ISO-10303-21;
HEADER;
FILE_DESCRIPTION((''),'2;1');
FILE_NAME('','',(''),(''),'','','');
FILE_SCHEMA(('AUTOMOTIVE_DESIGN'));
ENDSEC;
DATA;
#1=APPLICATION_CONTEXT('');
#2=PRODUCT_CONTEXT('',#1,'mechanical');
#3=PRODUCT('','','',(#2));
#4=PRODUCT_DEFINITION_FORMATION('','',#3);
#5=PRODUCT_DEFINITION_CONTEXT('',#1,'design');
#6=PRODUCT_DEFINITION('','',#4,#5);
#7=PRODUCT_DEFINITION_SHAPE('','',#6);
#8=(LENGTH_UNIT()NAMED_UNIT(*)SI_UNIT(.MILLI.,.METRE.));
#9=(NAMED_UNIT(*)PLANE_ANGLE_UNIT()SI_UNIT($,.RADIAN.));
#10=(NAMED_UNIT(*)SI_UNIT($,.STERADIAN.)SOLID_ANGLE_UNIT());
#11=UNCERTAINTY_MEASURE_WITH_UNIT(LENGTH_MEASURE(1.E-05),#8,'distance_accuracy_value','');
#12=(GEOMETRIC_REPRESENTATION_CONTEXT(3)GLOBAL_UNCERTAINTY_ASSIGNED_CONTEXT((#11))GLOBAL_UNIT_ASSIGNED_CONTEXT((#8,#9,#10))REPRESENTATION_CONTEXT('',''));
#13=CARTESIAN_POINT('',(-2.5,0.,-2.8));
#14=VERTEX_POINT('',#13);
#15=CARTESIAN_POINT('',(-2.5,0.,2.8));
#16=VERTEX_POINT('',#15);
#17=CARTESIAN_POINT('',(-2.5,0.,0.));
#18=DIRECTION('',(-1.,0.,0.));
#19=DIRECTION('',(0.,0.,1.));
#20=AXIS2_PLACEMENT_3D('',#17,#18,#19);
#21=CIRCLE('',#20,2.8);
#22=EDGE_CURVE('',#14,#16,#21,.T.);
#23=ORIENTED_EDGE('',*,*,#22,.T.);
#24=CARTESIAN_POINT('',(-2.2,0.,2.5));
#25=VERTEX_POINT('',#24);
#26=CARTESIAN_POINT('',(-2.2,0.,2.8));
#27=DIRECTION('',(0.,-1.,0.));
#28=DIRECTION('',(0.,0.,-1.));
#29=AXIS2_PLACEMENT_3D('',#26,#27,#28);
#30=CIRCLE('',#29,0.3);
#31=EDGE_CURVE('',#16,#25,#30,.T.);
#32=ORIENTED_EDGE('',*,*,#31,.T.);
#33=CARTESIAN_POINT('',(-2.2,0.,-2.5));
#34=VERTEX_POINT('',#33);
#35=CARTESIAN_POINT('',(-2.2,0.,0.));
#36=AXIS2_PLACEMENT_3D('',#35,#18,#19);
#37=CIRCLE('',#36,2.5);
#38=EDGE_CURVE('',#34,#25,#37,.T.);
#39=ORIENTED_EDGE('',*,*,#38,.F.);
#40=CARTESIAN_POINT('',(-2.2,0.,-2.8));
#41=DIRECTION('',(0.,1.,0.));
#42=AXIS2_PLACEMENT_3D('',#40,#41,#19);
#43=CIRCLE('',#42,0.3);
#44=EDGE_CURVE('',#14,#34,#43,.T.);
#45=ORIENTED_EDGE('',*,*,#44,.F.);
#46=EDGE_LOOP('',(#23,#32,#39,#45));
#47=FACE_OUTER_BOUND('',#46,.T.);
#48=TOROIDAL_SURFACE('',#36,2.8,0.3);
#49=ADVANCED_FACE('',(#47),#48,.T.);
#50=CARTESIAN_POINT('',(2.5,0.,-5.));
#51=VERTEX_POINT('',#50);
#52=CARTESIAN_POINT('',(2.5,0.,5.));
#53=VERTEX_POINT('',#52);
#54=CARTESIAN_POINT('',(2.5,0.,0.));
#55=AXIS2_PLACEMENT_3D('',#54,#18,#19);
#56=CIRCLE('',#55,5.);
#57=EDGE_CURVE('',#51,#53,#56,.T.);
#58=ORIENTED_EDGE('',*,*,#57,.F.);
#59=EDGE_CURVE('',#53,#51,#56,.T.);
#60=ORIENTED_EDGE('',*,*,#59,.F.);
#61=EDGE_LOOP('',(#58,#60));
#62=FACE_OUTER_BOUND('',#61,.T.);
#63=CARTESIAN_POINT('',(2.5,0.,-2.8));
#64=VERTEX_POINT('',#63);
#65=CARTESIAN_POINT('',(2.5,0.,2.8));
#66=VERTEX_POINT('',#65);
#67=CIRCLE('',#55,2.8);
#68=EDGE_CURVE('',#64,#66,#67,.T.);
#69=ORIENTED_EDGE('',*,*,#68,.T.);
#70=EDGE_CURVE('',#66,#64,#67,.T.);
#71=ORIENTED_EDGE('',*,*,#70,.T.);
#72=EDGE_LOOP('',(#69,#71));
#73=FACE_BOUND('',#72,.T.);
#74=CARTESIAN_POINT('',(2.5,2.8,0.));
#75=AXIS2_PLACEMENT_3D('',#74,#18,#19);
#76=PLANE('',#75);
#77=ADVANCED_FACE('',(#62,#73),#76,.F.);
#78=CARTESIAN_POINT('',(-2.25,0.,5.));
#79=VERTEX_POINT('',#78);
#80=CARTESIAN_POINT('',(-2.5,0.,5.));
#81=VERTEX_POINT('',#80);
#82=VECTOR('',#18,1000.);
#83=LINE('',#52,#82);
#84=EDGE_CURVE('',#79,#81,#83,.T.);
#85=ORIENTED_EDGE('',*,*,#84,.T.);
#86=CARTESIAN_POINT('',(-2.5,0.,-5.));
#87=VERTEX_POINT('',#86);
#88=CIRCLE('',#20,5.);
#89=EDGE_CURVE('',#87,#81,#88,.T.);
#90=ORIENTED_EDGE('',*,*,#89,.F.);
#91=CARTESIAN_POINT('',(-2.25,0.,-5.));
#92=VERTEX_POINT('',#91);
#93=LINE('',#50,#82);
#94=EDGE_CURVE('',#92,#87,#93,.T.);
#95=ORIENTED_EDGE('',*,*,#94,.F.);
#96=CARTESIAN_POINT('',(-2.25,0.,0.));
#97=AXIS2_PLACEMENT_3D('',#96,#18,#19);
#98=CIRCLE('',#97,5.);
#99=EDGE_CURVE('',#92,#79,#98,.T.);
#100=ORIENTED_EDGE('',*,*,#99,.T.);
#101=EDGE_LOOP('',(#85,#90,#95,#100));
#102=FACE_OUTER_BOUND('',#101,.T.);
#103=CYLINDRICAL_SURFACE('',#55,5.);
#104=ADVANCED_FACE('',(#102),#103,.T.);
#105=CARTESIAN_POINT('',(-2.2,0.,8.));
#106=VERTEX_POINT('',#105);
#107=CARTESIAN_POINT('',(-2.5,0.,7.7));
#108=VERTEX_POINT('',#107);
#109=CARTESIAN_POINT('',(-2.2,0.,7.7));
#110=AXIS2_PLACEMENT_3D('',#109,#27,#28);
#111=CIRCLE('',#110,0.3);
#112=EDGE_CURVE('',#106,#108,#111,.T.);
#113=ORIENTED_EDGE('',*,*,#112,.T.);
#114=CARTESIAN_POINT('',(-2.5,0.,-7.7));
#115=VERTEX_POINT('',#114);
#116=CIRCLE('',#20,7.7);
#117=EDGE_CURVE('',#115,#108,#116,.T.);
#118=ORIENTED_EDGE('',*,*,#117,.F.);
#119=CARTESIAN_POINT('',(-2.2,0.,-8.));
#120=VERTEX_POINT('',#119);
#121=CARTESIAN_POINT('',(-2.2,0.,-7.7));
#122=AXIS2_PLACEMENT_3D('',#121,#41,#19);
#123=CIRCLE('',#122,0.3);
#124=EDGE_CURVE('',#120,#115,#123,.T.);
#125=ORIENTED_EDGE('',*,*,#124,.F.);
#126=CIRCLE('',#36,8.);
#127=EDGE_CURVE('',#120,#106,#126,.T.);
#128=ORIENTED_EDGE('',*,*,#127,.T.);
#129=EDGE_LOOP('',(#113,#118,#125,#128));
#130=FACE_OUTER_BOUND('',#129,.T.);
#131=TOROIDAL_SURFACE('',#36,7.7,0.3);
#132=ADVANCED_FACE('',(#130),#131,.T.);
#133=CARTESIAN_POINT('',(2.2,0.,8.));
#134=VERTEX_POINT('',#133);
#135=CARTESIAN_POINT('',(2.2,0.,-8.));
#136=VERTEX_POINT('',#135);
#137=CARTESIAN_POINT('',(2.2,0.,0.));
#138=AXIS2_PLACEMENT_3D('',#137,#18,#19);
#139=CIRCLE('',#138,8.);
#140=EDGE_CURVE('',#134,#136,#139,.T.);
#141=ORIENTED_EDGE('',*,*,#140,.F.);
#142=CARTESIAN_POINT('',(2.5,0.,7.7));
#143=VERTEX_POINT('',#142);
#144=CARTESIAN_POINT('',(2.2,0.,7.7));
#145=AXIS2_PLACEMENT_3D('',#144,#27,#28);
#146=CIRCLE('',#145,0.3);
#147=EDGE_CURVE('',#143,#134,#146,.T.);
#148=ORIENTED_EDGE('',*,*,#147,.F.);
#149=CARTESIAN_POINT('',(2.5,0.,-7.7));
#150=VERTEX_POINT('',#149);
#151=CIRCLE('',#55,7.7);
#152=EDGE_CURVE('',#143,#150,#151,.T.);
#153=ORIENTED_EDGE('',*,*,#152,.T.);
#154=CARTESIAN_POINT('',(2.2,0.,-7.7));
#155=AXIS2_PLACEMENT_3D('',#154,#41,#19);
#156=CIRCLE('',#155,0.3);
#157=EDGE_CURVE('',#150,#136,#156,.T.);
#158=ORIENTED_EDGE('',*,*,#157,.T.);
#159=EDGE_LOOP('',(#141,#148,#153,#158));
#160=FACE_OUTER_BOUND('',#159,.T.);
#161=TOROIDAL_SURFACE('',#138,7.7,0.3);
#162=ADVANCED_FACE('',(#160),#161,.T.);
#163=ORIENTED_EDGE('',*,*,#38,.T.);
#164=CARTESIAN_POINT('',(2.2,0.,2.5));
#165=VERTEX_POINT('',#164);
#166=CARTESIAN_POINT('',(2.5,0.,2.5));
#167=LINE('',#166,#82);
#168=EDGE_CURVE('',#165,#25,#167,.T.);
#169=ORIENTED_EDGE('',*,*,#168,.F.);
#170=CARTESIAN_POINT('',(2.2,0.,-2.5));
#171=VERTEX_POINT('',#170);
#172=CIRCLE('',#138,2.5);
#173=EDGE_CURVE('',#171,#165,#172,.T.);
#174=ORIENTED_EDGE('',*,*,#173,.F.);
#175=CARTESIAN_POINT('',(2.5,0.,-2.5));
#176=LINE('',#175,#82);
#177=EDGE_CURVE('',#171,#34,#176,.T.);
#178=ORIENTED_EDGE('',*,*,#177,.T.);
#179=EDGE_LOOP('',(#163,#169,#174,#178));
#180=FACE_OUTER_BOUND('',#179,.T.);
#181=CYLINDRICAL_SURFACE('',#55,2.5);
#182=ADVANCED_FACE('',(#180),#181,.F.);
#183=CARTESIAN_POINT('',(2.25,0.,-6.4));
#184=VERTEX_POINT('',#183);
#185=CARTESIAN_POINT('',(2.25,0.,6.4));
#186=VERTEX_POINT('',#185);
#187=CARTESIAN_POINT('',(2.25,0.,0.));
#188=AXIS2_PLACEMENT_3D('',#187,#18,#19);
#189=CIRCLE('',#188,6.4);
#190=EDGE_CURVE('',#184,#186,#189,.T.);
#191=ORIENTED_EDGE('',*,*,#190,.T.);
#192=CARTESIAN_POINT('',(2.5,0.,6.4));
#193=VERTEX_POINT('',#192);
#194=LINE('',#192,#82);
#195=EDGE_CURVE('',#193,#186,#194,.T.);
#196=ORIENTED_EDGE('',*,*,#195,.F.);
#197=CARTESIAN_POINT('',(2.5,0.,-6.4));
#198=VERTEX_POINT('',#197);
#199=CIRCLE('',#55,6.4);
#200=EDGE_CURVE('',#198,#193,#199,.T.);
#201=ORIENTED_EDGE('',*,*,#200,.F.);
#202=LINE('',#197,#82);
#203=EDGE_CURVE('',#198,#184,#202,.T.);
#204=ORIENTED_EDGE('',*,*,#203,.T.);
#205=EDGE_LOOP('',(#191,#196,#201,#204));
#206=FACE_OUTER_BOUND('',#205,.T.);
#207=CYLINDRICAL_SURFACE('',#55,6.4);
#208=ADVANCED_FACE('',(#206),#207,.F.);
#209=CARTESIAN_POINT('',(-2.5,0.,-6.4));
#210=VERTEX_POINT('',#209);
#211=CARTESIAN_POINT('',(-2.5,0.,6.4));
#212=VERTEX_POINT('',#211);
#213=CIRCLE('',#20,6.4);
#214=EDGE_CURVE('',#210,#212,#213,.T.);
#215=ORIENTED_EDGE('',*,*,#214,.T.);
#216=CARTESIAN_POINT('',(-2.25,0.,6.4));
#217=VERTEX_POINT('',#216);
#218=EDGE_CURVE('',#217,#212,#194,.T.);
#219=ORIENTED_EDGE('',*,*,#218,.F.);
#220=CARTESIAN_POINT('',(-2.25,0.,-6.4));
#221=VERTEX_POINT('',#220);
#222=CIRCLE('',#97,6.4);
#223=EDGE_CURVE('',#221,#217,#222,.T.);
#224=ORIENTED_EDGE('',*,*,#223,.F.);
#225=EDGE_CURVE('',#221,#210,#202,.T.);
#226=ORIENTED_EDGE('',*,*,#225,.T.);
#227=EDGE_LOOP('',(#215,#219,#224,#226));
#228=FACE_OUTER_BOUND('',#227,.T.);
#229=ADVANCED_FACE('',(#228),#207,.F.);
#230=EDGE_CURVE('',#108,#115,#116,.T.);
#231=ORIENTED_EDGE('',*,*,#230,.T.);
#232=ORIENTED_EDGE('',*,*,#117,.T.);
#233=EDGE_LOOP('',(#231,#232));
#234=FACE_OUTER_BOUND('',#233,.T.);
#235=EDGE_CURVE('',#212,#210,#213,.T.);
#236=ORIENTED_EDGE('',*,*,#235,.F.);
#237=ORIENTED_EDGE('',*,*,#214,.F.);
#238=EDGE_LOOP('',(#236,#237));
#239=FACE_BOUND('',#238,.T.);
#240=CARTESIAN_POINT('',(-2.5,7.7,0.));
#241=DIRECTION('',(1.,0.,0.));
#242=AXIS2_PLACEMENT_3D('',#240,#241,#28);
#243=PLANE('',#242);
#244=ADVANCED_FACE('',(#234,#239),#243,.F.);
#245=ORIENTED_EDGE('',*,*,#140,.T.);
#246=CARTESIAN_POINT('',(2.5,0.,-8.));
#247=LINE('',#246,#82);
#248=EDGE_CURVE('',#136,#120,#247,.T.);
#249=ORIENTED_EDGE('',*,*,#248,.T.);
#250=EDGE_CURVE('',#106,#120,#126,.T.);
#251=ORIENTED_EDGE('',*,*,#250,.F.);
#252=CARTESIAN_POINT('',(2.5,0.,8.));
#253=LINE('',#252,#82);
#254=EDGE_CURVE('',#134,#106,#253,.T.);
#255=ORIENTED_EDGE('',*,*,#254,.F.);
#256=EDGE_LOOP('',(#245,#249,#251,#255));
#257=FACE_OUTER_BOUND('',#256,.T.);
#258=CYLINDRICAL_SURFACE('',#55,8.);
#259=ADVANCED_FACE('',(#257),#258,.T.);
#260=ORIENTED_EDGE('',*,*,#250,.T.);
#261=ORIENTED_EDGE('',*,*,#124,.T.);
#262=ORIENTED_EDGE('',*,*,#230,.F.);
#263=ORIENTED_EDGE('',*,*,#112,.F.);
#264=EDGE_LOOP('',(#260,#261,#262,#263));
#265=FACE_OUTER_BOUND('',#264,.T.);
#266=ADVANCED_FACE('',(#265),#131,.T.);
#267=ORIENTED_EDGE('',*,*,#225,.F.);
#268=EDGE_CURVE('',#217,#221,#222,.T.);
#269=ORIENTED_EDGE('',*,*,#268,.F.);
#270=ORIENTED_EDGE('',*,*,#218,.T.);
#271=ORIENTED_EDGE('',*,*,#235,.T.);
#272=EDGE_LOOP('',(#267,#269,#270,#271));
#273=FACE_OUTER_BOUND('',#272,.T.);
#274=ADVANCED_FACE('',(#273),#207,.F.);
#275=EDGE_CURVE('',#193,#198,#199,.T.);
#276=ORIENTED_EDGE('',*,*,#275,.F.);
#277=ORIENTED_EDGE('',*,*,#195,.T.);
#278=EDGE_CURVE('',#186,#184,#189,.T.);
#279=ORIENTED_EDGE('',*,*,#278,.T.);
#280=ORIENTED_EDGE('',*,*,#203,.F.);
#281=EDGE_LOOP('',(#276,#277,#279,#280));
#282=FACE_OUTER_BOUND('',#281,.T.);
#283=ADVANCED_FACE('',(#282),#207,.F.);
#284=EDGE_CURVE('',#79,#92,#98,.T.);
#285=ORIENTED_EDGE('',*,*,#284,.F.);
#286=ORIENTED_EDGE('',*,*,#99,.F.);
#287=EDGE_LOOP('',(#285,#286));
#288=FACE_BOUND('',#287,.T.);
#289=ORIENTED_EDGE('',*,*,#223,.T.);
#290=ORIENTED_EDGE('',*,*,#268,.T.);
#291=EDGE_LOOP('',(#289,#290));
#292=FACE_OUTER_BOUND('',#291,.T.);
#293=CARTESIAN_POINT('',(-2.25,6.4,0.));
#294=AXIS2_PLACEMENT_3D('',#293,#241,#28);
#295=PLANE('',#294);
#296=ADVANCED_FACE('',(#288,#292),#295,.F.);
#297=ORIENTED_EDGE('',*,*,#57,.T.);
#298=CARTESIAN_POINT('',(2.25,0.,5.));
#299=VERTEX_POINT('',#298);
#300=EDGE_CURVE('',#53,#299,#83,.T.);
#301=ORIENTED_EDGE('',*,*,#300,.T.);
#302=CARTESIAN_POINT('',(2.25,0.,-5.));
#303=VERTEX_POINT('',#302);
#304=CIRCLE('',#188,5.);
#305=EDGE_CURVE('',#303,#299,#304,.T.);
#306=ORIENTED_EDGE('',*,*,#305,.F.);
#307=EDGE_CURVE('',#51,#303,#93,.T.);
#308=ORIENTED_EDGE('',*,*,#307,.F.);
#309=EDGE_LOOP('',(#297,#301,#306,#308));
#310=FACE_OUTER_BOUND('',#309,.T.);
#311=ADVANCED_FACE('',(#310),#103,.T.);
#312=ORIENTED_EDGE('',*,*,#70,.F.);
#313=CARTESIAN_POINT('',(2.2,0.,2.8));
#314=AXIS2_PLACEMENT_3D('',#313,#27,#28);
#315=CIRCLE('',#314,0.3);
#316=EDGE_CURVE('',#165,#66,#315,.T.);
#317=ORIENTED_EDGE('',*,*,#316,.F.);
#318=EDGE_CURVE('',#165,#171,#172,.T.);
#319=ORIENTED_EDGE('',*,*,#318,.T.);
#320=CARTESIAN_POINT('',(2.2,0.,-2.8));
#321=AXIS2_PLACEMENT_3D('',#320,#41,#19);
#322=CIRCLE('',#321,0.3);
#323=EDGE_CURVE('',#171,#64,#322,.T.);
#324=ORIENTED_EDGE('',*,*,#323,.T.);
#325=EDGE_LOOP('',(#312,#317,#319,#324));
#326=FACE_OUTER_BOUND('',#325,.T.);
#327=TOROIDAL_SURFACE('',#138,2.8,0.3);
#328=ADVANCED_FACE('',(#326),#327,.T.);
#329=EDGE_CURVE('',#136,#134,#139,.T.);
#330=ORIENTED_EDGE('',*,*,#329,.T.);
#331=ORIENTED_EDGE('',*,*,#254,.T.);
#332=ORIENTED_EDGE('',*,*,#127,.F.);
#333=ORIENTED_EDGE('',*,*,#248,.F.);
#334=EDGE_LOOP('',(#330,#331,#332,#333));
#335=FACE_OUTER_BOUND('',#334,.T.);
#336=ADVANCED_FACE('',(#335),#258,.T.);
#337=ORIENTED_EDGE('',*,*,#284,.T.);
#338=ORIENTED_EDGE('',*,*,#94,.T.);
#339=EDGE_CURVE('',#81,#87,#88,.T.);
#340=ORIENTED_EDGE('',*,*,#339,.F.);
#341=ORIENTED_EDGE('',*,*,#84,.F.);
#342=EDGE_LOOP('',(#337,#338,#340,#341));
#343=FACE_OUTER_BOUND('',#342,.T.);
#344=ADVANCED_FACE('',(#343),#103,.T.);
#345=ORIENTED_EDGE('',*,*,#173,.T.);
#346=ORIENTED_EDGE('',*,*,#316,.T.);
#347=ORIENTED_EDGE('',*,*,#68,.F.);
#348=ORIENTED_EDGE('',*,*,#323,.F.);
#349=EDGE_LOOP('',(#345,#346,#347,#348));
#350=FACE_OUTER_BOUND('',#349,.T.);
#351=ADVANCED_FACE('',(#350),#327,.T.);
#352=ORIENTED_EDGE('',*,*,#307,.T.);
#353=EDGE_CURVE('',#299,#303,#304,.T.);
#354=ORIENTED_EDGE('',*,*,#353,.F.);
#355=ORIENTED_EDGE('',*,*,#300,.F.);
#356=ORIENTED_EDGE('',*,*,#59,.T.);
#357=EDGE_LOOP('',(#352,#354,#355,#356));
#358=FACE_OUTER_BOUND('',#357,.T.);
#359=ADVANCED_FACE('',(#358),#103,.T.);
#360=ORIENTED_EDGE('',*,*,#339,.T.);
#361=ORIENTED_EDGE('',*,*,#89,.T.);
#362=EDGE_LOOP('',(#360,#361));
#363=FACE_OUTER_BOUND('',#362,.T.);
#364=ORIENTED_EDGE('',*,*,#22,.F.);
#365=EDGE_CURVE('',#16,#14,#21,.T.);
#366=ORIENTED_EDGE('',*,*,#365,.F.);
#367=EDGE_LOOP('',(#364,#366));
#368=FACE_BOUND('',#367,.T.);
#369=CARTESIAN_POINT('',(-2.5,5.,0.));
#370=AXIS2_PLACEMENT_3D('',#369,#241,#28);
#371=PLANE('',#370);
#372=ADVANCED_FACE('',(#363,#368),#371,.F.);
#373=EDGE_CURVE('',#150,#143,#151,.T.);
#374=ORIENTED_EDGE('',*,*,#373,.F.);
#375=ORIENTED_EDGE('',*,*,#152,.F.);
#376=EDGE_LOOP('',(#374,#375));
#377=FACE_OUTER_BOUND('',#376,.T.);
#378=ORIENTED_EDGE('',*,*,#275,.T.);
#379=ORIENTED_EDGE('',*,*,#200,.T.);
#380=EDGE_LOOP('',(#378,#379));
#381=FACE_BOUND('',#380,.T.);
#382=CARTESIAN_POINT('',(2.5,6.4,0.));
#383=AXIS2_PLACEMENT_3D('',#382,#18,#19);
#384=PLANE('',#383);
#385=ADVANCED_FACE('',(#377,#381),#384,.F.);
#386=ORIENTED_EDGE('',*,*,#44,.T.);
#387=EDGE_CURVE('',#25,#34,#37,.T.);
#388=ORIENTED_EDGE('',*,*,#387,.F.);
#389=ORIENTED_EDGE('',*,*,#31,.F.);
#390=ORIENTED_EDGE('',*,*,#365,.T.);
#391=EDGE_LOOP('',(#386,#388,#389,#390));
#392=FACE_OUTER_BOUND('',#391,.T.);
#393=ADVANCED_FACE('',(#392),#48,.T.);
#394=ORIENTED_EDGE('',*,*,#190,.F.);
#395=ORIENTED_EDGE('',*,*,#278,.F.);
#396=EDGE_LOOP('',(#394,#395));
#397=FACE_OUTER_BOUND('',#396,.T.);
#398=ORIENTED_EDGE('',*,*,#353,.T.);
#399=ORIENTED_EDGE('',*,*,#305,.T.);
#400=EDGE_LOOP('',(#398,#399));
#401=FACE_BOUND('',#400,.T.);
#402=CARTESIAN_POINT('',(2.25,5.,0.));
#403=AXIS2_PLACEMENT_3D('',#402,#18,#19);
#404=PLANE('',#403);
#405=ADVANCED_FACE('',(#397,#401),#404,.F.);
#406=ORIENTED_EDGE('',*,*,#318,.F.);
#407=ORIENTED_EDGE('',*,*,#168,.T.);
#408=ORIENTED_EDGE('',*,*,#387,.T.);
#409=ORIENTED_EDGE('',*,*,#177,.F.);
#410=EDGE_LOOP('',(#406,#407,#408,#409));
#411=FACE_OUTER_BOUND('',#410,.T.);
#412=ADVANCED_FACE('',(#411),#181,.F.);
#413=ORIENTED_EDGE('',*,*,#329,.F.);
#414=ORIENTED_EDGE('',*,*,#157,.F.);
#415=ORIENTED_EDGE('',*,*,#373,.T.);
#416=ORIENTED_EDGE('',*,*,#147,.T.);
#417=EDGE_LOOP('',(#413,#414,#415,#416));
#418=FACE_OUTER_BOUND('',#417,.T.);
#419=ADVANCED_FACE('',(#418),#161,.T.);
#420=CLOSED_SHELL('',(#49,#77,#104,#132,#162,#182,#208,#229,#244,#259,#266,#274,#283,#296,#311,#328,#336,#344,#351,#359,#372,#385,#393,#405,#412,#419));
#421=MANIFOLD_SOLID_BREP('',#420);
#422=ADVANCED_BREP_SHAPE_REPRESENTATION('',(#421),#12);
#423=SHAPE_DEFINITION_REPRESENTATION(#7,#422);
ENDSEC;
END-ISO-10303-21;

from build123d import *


with BuildPart() as part:
    # 草图1 → 旋转1 (revolve)
    with BuildSketch(Plane.XY, mode=Mode.PRIVATE) as revolve_1_sk:
        with BuildLine():
            Line((-2.5, 7.7), (-2.5, 6.4))
            Line((-2.5, 6.4), (-2.25, 6.4))
            Line((-2.25, 6.4), (-2.25, 5))
            Line((-2.25, 5), (-2.5, 5))
            Line((-2.5, 5), (-2.5, 2.8))
            ThreePointArc((-2.5, 2.8), (-2.412132034, 2.587867966), (-2.2, 2.5))
            Line((-2.2, 2.5), (2.2, 2.5))
            ThreePointArc((2.2, 2.5), (2.412132034, 2.587867966), (2.5, 2.8))
            Line((2.5, 2.8), (2.5, 5))
            Line((2.5, 5), (2.25, 5))
            Line((2.25, 5), (2.25, 6.4))
            Line((2.25, 6.4), (2.5, 6.4))
            Line((2.5, 6.4), (2.5, 7.7))
            ThreePointArc((2.5, 7.7), (2.412132034, 7.912132034), (2.2, 8))
            Line((2.2, 8), (-2.2, 8))
            ThreePointArc((-2.2, 8), (-2.412132034, 7.912132034), (-2.5, 7.7))
        make_face()
    revolve(revolve_1_sk.sketch.rotate(Axis((2.5, 0, 0), (-1, 0, 0)), 270), axis=Axis((2.5, 0, 0), (-1, 0, 0)))


solid = part.part
